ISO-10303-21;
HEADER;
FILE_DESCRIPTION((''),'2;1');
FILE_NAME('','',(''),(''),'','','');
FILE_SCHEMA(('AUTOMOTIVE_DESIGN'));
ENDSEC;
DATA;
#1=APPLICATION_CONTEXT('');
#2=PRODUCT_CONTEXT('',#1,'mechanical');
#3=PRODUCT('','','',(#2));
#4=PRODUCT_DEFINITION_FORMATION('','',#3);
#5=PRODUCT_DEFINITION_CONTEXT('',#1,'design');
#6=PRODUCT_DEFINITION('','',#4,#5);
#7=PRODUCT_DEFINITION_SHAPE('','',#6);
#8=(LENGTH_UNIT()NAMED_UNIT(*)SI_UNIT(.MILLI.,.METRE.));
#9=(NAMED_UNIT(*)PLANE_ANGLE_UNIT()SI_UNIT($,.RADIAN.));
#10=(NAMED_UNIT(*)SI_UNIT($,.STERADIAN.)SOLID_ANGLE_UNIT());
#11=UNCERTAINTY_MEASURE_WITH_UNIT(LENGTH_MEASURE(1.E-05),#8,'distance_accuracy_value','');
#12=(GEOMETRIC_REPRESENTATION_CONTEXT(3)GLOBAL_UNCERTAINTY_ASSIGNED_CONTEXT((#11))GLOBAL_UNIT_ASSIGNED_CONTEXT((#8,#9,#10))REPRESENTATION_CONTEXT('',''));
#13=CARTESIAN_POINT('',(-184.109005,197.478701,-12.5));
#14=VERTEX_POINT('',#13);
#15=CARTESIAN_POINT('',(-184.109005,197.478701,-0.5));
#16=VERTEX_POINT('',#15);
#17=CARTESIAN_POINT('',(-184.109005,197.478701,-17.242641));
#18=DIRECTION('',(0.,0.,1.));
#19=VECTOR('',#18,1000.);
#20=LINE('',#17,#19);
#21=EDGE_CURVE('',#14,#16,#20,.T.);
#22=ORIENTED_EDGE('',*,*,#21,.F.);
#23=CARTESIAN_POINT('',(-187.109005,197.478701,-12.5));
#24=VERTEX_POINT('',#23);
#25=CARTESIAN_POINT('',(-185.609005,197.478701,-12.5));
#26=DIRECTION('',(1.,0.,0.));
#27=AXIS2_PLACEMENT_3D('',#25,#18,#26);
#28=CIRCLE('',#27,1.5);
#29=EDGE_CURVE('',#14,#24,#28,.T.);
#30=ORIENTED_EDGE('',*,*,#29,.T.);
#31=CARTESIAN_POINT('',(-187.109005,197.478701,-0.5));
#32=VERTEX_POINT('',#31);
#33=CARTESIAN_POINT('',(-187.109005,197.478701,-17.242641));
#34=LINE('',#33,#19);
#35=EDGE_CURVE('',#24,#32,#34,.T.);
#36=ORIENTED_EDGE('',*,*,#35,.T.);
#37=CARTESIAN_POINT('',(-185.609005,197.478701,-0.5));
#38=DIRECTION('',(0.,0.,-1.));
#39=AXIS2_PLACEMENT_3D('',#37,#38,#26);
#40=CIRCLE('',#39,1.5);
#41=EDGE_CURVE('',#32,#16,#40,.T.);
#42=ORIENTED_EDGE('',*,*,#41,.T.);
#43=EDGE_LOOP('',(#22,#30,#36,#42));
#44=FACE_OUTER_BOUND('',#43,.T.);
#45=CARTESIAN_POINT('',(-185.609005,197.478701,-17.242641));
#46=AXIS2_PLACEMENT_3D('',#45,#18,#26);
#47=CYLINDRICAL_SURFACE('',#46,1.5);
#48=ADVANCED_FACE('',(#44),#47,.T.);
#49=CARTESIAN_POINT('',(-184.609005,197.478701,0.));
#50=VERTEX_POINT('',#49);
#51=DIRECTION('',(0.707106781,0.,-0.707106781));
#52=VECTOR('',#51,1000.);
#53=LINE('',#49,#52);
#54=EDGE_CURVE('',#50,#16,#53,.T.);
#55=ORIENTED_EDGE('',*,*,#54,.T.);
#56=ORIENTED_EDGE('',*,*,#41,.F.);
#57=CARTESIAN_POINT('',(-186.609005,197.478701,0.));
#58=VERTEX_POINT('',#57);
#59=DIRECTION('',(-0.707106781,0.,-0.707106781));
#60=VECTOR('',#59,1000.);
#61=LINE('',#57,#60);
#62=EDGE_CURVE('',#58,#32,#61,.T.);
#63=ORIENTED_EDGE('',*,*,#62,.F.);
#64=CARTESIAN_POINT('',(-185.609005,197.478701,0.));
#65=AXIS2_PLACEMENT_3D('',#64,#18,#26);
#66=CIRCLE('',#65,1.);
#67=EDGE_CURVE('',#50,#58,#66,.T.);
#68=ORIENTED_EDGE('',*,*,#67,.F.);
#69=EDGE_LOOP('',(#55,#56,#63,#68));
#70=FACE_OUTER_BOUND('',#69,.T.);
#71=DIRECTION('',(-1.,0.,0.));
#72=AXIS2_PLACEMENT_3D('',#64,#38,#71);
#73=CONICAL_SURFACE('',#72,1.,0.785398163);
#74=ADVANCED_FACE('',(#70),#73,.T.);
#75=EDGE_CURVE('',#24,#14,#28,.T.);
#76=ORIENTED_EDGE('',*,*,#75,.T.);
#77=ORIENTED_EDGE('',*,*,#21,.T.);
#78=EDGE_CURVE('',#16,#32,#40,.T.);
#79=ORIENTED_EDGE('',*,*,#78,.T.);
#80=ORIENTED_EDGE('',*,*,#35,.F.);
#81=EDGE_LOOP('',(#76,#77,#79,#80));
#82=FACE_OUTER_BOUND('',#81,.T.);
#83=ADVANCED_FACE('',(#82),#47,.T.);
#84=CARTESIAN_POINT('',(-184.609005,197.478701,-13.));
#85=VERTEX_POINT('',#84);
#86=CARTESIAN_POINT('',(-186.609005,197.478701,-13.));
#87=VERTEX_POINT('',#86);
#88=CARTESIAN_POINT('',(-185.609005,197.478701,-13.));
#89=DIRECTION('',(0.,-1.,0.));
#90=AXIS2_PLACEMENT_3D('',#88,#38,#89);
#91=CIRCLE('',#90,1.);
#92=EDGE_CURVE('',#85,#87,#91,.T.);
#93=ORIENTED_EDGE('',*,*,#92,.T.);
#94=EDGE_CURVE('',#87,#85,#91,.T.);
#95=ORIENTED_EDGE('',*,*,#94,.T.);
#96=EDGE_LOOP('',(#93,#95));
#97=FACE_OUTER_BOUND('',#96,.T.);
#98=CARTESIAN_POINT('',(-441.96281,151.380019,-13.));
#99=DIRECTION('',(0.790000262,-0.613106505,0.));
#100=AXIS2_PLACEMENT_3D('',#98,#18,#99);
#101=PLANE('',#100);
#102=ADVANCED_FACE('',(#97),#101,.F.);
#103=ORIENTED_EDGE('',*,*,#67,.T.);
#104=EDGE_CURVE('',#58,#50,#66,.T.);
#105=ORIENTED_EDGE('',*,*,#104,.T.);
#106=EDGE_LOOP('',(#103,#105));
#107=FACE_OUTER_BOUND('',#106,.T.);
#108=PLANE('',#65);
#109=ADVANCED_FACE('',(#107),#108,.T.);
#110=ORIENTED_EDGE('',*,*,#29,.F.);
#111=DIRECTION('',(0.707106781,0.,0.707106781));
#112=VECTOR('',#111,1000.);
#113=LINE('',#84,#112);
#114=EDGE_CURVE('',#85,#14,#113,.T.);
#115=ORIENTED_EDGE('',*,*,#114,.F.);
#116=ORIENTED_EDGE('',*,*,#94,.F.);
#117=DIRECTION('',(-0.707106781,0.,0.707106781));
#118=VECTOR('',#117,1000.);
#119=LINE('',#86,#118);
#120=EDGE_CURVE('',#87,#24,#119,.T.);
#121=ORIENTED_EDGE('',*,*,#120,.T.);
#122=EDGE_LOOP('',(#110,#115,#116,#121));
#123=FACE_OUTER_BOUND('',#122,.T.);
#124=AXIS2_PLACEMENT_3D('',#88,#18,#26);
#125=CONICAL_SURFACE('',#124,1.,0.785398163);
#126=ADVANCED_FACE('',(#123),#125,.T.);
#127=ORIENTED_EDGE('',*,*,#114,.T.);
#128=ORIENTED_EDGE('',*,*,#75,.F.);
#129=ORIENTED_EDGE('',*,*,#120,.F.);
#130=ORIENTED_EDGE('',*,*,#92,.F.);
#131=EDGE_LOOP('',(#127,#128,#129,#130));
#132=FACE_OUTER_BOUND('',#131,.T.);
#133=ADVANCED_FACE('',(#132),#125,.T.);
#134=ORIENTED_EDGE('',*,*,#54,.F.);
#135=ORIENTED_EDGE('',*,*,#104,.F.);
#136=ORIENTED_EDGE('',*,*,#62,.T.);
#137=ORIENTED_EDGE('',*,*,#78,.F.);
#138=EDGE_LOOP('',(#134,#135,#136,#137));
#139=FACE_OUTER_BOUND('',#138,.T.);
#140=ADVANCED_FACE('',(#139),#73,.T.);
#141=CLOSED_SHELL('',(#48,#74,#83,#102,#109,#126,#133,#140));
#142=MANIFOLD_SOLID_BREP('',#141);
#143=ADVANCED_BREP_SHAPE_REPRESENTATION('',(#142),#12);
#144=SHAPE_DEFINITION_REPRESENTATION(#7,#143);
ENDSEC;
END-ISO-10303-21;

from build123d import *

# Parameters (mm, degrees)
SKETCH_1_R      = 1.5
EXTRUDE_1_DEPTH = 13
CHAMFER_1_SIZE  = 0.5


with BuildPart() as part:
    # 草图1 → 凸台-拉伸1 (new body)
    with BuildSketch(Plane.XY):
        with Locations((-185.609004659, 197.47870093)):
            Circle(SKETCH_1_R)
    extrude(amount=-EXTRUDE_1_DEPTH)

    # 倒角1
    chamfer_1_edges = [part.edges().sort_by_distance(p)[0] for p in [
        (-187.109004659, 197.47870093, 0),
        (-187.109004659, 197.47870093, -13),
    ]]
    chamfer(chamfer_1_edges, length=CHAMFER_1_SIZE)


solid = part.part
